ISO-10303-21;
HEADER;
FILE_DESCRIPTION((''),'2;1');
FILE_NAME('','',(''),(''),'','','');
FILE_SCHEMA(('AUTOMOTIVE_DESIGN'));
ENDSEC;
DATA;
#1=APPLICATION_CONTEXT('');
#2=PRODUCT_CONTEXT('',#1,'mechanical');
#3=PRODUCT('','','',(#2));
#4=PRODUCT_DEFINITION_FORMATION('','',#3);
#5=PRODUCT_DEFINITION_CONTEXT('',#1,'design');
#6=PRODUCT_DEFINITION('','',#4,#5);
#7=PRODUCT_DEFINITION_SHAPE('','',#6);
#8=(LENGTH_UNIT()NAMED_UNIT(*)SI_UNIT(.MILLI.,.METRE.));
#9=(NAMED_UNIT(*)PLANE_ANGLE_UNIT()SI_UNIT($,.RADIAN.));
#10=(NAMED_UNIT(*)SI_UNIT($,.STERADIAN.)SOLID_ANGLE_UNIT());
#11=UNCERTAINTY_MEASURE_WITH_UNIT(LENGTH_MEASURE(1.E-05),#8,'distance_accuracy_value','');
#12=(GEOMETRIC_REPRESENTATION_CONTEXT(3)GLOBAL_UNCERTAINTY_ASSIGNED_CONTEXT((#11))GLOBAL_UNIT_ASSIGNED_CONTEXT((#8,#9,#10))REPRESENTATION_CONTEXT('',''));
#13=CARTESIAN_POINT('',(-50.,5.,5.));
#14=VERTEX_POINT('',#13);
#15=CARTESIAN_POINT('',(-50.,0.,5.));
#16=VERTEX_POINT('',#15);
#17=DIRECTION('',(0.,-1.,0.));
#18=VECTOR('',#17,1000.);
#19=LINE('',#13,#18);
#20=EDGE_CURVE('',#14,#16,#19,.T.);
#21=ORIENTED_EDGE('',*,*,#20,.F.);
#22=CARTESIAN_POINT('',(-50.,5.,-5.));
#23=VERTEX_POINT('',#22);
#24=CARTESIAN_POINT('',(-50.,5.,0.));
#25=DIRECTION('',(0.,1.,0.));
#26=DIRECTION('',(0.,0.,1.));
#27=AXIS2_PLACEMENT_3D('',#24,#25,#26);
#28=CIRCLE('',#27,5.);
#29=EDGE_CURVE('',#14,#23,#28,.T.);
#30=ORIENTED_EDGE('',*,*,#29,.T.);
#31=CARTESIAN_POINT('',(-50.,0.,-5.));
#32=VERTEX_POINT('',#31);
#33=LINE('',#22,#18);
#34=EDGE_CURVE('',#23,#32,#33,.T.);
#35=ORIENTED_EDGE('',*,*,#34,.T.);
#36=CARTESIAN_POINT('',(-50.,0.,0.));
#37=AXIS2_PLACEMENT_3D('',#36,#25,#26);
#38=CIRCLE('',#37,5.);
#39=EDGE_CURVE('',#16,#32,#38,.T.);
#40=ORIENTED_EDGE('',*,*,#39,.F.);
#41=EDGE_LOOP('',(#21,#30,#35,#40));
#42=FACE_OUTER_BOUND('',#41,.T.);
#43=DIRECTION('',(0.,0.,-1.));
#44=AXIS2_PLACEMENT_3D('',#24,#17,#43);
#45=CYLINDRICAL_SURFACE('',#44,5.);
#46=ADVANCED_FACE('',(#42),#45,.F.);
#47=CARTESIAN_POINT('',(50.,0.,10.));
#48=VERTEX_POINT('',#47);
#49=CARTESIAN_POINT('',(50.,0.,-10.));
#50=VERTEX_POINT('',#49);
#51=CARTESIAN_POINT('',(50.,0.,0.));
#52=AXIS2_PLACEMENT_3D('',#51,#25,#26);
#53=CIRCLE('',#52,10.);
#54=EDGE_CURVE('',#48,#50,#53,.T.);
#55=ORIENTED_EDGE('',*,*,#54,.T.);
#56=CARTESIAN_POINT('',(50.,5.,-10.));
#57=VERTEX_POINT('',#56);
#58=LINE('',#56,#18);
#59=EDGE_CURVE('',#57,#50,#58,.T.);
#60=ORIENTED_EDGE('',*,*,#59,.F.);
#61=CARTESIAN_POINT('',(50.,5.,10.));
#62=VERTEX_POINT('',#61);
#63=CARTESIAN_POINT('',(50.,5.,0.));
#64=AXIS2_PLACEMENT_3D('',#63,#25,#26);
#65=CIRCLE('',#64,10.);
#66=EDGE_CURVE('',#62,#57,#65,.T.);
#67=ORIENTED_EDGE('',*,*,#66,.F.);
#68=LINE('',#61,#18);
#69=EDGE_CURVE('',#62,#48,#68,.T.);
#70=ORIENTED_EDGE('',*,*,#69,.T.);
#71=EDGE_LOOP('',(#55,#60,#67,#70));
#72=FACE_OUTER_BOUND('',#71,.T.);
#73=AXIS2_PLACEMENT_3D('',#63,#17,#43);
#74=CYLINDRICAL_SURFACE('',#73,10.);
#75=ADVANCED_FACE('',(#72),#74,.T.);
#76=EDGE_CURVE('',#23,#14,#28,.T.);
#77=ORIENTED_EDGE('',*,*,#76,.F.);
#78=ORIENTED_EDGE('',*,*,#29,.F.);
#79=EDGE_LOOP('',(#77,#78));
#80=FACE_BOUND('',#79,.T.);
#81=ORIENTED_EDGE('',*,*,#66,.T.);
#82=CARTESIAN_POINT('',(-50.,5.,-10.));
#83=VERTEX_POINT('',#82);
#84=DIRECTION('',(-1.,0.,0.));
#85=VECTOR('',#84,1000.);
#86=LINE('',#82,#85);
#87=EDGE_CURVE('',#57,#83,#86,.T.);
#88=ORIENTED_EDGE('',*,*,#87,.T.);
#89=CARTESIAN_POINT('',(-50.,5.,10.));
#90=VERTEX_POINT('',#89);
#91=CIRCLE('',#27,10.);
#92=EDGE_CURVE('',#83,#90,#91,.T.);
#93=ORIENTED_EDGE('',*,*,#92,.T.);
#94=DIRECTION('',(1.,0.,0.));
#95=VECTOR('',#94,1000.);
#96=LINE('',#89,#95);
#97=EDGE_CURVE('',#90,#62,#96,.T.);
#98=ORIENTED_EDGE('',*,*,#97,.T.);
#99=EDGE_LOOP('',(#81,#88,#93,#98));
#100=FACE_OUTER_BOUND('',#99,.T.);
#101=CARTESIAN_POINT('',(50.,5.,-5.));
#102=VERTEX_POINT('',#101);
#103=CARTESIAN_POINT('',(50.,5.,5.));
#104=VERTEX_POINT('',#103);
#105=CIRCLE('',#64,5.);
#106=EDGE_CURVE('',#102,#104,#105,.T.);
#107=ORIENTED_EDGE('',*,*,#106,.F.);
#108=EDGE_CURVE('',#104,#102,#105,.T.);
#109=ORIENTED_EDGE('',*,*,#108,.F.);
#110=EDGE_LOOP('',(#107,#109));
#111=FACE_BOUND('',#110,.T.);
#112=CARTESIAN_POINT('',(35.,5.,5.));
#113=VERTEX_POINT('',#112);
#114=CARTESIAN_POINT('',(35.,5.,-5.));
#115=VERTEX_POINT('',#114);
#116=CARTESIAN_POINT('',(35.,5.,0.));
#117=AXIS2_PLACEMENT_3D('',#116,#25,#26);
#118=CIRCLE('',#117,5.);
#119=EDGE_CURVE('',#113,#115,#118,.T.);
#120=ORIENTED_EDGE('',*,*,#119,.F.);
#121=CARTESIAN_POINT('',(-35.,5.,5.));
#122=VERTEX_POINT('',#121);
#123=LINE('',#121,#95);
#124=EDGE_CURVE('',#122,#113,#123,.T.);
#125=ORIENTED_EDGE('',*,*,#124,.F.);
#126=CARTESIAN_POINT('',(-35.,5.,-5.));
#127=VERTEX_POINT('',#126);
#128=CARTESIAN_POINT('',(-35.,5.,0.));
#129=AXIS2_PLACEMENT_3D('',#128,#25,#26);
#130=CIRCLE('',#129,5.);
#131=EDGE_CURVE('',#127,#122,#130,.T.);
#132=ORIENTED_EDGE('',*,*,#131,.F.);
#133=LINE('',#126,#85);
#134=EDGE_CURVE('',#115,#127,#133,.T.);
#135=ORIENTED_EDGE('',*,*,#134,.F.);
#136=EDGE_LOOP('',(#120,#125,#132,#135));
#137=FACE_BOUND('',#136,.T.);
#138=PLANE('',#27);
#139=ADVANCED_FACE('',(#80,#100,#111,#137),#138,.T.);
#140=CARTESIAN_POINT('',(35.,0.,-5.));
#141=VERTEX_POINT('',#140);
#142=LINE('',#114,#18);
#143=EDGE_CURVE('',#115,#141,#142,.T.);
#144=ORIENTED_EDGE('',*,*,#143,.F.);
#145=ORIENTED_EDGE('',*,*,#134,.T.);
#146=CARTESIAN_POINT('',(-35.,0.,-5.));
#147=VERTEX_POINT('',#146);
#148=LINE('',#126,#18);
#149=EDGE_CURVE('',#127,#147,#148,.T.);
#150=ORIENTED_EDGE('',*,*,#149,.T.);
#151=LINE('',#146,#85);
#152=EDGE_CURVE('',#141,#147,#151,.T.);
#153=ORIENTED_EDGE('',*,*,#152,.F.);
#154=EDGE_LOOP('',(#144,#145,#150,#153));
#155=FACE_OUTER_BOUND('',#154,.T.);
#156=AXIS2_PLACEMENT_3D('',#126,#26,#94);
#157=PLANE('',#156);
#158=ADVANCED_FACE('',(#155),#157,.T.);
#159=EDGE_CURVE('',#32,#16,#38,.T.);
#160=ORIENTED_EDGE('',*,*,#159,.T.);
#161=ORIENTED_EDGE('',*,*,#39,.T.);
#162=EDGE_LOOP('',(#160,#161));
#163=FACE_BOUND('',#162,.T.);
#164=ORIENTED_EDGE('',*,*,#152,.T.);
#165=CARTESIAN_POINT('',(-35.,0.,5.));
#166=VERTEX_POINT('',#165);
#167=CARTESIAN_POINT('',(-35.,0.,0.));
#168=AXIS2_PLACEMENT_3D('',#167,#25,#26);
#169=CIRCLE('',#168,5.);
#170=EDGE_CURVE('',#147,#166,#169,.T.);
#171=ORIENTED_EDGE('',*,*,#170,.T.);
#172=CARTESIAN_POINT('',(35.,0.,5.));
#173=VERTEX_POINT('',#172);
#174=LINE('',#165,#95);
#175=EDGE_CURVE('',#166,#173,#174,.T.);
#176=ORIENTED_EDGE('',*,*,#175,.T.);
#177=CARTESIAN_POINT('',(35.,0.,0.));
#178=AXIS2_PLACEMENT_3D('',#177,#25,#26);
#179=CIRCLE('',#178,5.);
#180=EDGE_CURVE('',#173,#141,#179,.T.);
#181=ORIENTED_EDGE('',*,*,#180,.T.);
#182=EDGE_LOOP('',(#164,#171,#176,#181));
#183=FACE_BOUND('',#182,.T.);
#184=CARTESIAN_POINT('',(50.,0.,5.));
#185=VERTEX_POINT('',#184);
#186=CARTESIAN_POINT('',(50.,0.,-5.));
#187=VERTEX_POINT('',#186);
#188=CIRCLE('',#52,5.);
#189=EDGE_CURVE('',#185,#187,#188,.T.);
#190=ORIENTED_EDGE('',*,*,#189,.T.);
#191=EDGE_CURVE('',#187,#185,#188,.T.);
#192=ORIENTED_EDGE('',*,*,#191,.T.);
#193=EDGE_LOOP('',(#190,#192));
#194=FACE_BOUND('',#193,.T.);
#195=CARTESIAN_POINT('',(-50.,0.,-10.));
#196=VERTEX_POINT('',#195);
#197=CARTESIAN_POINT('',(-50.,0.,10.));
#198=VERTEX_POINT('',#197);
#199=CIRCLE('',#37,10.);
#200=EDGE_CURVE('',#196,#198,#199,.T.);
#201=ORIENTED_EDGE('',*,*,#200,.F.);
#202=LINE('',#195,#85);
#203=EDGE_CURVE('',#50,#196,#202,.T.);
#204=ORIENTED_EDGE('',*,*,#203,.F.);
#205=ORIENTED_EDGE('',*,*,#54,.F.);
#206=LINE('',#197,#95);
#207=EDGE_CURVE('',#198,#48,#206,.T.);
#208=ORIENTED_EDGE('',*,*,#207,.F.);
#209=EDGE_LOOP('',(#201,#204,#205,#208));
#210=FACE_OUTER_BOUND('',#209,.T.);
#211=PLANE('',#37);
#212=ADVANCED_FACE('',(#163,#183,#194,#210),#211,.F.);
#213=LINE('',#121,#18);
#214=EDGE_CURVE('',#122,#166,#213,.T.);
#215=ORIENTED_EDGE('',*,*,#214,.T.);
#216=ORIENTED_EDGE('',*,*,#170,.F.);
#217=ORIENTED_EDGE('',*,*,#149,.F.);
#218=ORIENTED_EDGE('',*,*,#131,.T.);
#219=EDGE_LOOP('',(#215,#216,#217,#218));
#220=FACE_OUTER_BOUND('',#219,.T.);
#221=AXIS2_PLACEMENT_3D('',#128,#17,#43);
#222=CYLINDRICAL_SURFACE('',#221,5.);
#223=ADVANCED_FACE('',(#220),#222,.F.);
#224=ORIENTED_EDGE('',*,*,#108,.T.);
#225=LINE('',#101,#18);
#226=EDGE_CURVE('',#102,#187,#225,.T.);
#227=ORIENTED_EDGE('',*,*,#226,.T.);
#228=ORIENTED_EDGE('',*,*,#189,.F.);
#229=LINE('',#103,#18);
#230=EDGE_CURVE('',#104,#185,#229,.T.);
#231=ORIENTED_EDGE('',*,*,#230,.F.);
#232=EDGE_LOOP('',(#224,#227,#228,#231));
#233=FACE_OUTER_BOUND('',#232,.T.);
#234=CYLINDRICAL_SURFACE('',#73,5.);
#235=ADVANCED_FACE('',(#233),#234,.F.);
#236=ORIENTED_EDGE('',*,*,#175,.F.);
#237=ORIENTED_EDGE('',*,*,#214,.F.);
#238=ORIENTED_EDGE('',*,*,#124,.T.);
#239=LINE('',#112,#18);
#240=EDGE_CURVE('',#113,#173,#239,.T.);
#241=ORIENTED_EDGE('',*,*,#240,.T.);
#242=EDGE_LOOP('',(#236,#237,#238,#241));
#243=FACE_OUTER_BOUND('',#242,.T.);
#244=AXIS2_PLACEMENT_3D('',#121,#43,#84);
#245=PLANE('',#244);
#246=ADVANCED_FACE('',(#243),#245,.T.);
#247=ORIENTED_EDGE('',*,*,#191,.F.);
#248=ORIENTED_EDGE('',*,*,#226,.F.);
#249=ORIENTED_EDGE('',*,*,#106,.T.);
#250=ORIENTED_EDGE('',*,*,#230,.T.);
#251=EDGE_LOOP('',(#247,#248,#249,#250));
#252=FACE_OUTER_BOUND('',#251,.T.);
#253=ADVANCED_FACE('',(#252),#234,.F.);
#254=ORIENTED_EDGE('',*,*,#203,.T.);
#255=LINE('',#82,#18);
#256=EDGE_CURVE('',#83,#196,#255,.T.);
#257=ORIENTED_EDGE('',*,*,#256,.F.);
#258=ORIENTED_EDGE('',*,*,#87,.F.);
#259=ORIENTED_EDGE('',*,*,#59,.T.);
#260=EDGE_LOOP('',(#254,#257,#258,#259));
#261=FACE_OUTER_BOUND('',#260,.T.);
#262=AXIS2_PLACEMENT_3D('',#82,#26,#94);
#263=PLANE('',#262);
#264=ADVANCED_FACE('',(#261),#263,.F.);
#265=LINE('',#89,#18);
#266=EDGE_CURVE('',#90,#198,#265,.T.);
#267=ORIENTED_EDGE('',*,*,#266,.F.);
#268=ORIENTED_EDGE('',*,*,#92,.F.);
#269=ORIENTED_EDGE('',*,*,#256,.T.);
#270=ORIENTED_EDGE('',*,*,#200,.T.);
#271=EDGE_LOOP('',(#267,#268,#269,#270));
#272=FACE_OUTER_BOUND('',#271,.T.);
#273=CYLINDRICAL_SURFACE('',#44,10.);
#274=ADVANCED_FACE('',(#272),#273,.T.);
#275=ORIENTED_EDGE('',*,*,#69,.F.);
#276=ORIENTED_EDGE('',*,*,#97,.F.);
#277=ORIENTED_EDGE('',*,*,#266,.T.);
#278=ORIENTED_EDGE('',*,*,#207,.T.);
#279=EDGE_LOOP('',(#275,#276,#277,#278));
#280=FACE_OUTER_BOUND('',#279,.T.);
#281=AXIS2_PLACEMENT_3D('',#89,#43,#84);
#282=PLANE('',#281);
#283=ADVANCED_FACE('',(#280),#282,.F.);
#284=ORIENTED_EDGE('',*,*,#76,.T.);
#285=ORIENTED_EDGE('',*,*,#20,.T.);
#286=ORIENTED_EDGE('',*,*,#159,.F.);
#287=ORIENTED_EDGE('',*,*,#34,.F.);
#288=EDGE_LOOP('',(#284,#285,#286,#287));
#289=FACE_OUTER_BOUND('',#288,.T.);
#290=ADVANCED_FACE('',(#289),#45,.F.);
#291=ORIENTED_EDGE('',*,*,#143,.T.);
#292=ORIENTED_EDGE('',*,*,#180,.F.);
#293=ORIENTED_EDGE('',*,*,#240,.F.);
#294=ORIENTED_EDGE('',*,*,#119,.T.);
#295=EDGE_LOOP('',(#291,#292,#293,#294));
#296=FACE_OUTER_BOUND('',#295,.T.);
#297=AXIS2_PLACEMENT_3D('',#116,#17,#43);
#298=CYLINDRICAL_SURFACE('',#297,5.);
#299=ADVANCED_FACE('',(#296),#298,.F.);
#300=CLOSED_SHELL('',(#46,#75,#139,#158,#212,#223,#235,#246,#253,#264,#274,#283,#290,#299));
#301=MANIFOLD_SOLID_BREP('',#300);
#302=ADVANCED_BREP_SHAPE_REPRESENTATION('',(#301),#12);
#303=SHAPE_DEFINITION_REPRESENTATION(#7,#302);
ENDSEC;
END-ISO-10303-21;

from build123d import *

# Parameters (mm, degrees)
LINK_PROFILE_SKETCH_R = 5
LINK_PLATE_5MM_DEPTH  = 5


with BuildPart() as part:
    # Link Profile Sketch → Link Plate 5mm (new body)
    with BuildSketch(Plane(origin=(0, 0, 0), x_dir=(1, 0, 0), z_dir=(0, 1, 0))):
        with BuildLine():
            Line((-50, 10), (50, 10))
            ThreePointArc((50, 10), (60, 0), (50, -10))
            Line((50, -10), (-50, -10))
            ThreePointArc((-50, -10), (-60, 0), (-50, 10))
        make_face()
        with Locations(Location((-50, 0, 0), (0, 0, 270))):
            Circle(LINK_PROFILE_SKETCH_R, mode=Mode.SUBTRACT)
        with Locations(Location((50, 0, 0), (0, 0, 270))):
            Circle(LINK_PROFILE_SKETCH_R, mode=Mode.SUBTRACT)
        with BuildLine():
            Line((-35, 5), (35, 5))
            ThreePointArc((35, 5), (40, 0), (35, -5))
            Line((35, -5), (-35, -5))
            ThreePointArc((-35, -5), (-40, 0), (-35, 5))
        make_face(mode=Mode.SUBTRACT)
    extrude(amount=LINK_PLATE_5MM_DEPTH)


solid = part.part
